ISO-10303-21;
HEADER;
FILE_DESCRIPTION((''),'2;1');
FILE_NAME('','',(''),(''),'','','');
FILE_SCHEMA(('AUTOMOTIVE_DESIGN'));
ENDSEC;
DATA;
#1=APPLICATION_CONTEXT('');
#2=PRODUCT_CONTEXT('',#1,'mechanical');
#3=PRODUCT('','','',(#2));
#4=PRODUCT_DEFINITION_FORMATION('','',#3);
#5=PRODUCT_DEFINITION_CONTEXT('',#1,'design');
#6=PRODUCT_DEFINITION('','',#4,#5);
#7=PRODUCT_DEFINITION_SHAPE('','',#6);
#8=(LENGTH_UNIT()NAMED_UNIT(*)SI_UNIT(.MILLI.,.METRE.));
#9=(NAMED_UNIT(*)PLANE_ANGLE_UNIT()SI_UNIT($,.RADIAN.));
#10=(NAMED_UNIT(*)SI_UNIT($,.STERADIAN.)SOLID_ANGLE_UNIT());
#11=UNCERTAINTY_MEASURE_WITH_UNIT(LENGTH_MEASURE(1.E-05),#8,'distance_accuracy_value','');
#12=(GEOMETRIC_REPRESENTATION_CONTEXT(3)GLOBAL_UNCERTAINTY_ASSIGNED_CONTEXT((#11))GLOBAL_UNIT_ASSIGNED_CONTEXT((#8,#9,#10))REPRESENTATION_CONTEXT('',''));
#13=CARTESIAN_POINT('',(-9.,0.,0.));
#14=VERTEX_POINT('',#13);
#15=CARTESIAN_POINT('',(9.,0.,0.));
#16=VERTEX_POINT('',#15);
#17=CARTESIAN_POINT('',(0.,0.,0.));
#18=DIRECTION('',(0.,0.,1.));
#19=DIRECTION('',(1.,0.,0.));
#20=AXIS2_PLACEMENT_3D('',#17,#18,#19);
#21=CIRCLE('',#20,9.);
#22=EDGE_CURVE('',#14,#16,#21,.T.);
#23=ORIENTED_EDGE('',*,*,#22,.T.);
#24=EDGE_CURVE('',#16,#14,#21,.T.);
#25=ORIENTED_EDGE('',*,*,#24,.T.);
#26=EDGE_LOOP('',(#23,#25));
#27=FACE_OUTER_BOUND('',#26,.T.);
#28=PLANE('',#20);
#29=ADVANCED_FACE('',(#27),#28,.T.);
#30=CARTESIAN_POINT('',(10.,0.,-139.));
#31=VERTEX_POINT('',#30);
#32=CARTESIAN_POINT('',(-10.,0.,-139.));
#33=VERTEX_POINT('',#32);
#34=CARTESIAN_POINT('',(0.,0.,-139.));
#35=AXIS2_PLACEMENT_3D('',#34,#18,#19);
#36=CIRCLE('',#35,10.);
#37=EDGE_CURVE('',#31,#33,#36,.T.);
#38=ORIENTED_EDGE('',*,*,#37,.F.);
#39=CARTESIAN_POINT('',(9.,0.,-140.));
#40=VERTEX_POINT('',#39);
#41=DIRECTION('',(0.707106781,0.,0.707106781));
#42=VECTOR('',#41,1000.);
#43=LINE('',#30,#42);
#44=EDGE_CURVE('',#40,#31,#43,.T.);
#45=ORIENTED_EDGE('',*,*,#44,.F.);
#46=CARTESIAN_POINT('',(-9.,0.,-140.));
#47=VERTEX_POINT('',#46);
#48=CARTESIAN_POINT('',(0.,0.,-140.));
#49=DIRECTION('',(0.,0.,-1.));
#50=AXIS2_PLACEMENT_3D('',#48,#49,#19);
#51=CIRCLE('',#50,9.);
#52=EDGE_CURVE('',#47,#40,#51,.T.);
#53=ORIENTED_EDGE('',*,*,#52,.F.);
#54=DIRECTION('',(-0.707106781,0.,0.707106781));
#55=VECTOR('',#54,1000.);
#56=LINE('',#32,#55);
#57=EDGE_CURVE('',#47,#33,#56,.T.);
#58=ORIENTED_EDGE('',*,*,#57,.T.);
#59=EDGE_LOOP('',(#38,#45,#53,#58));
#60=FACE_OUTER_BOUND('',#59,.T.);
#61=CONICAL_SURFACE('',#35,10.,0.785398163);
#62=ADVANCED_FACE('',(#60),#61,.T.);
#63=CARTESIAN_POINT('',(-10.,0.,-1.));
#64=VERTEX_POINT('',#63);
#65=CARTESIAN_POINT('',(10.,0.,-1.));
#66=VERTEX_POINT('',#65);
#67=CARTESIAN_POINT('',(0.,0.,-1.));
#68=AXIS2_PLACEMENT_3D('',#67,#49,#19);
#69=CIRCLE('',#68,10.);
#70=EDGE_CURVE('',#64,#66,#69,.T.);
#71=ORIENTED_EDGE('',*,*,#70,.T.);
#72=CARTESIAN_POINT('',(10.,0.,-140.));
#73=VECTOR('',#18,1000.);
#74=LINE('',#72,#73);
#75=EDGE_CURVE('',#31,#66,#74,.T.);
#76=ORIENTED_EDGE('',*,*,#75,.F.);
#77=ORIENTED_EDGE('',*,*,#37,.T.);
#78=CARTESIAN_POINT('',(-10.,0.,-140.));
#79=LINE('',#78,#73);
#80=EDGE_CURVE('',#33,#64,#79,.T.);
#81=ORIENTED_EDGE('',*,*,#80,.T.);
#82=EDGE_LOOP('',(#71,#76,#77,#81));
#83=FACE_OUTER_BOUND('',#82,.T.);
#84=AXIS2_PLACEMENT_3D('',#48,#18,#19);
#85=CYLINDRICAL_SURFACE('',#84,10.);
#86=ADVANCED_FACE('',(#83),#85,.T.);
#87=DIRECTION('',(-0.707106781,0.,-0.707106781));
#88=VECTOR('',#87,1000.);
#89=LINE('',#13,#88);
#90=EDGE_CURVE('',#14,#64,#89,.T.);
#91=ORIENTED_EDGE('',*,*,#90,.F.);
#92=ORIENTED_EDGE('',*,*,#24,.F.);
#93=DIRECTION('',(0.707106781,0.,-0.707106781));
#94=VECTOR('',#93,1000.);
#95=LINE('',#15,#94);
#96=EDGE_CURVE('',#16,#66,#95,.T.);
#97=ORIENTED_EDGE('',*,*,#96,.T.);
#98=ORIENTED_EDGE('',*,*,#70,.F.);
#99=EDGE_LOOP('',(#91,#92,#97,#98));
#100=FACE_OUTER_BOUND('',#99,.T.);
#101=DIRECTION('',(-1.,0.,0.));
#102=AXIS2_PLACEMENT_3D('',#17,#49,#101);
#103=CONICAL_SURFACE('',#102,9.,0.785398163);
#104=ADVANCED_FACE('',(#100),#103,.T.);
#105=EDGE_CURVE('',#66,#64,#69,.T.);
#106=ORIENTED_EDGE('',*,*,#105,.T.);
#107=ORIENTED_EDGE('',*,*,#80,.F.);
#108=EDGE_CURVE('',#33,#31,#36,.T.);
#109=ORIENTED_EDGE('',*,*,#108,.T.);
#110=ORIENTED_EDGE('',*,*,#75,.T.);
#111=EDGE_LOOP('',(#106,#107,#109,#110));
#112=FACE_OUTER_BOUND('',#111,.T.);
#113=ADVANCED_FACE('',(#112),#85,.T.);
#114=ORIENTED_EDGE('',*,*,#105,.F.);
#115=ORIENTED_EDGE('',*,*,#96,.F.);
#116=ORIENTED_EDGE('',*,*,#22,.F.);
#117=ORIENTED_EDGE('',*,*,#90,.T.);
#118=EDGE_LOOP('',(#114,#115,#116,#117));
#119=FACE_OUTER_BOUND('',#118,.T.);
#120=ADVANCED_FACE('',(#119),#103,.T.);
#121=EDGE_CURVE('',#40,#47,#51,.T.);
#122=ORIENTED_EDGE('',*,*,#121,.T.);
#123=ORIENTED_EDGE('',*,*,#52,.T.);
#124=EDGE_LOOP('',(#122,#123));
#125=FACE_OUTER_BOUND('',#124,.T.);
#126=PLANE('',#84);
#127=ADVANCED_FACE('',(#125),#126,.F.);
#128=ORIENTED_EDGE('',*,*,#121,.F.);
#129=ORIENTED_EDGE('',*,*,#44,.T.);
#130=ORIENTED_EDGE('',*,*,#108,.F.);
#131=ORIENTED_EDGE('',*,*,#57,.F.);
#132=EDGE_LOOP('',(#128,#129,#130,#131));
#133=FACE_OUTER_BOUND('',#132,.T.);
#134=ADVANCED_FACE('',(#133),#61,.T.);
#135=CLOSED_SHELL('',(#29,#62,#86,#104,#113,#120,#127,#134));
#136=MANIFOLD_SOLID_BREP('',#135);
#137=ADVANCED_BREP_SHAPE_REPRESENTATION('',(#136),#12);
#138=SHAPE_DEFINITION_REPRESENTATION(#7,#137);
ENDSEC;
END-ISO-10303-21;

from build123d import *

# Parameters (mm, degrees)
SKETCH1_R           = 10
BOSS_EXTRUDE1_DEPTH = 140
CHAMFER2_SIZE       = 1


with BuildPart() as part:
    # Sketch1 → Boss-Extrude1 (new body)
    with BuildSketch(Plane.XY):
        Circle(SKETCH1_R)
    extrude(amount=-BOSS_EXTRUDE1_DEPTH)

    # Chamfer2
    chamfer2_edges = [part.edges().sort_by_distance(p)[0] for p in [
        (-10, 0, 0),
        (-10, 0, -140),
    ]]
    chamfer(chamfer2_edges, length=CHAMFER2_SIZE)


solid = part.part
